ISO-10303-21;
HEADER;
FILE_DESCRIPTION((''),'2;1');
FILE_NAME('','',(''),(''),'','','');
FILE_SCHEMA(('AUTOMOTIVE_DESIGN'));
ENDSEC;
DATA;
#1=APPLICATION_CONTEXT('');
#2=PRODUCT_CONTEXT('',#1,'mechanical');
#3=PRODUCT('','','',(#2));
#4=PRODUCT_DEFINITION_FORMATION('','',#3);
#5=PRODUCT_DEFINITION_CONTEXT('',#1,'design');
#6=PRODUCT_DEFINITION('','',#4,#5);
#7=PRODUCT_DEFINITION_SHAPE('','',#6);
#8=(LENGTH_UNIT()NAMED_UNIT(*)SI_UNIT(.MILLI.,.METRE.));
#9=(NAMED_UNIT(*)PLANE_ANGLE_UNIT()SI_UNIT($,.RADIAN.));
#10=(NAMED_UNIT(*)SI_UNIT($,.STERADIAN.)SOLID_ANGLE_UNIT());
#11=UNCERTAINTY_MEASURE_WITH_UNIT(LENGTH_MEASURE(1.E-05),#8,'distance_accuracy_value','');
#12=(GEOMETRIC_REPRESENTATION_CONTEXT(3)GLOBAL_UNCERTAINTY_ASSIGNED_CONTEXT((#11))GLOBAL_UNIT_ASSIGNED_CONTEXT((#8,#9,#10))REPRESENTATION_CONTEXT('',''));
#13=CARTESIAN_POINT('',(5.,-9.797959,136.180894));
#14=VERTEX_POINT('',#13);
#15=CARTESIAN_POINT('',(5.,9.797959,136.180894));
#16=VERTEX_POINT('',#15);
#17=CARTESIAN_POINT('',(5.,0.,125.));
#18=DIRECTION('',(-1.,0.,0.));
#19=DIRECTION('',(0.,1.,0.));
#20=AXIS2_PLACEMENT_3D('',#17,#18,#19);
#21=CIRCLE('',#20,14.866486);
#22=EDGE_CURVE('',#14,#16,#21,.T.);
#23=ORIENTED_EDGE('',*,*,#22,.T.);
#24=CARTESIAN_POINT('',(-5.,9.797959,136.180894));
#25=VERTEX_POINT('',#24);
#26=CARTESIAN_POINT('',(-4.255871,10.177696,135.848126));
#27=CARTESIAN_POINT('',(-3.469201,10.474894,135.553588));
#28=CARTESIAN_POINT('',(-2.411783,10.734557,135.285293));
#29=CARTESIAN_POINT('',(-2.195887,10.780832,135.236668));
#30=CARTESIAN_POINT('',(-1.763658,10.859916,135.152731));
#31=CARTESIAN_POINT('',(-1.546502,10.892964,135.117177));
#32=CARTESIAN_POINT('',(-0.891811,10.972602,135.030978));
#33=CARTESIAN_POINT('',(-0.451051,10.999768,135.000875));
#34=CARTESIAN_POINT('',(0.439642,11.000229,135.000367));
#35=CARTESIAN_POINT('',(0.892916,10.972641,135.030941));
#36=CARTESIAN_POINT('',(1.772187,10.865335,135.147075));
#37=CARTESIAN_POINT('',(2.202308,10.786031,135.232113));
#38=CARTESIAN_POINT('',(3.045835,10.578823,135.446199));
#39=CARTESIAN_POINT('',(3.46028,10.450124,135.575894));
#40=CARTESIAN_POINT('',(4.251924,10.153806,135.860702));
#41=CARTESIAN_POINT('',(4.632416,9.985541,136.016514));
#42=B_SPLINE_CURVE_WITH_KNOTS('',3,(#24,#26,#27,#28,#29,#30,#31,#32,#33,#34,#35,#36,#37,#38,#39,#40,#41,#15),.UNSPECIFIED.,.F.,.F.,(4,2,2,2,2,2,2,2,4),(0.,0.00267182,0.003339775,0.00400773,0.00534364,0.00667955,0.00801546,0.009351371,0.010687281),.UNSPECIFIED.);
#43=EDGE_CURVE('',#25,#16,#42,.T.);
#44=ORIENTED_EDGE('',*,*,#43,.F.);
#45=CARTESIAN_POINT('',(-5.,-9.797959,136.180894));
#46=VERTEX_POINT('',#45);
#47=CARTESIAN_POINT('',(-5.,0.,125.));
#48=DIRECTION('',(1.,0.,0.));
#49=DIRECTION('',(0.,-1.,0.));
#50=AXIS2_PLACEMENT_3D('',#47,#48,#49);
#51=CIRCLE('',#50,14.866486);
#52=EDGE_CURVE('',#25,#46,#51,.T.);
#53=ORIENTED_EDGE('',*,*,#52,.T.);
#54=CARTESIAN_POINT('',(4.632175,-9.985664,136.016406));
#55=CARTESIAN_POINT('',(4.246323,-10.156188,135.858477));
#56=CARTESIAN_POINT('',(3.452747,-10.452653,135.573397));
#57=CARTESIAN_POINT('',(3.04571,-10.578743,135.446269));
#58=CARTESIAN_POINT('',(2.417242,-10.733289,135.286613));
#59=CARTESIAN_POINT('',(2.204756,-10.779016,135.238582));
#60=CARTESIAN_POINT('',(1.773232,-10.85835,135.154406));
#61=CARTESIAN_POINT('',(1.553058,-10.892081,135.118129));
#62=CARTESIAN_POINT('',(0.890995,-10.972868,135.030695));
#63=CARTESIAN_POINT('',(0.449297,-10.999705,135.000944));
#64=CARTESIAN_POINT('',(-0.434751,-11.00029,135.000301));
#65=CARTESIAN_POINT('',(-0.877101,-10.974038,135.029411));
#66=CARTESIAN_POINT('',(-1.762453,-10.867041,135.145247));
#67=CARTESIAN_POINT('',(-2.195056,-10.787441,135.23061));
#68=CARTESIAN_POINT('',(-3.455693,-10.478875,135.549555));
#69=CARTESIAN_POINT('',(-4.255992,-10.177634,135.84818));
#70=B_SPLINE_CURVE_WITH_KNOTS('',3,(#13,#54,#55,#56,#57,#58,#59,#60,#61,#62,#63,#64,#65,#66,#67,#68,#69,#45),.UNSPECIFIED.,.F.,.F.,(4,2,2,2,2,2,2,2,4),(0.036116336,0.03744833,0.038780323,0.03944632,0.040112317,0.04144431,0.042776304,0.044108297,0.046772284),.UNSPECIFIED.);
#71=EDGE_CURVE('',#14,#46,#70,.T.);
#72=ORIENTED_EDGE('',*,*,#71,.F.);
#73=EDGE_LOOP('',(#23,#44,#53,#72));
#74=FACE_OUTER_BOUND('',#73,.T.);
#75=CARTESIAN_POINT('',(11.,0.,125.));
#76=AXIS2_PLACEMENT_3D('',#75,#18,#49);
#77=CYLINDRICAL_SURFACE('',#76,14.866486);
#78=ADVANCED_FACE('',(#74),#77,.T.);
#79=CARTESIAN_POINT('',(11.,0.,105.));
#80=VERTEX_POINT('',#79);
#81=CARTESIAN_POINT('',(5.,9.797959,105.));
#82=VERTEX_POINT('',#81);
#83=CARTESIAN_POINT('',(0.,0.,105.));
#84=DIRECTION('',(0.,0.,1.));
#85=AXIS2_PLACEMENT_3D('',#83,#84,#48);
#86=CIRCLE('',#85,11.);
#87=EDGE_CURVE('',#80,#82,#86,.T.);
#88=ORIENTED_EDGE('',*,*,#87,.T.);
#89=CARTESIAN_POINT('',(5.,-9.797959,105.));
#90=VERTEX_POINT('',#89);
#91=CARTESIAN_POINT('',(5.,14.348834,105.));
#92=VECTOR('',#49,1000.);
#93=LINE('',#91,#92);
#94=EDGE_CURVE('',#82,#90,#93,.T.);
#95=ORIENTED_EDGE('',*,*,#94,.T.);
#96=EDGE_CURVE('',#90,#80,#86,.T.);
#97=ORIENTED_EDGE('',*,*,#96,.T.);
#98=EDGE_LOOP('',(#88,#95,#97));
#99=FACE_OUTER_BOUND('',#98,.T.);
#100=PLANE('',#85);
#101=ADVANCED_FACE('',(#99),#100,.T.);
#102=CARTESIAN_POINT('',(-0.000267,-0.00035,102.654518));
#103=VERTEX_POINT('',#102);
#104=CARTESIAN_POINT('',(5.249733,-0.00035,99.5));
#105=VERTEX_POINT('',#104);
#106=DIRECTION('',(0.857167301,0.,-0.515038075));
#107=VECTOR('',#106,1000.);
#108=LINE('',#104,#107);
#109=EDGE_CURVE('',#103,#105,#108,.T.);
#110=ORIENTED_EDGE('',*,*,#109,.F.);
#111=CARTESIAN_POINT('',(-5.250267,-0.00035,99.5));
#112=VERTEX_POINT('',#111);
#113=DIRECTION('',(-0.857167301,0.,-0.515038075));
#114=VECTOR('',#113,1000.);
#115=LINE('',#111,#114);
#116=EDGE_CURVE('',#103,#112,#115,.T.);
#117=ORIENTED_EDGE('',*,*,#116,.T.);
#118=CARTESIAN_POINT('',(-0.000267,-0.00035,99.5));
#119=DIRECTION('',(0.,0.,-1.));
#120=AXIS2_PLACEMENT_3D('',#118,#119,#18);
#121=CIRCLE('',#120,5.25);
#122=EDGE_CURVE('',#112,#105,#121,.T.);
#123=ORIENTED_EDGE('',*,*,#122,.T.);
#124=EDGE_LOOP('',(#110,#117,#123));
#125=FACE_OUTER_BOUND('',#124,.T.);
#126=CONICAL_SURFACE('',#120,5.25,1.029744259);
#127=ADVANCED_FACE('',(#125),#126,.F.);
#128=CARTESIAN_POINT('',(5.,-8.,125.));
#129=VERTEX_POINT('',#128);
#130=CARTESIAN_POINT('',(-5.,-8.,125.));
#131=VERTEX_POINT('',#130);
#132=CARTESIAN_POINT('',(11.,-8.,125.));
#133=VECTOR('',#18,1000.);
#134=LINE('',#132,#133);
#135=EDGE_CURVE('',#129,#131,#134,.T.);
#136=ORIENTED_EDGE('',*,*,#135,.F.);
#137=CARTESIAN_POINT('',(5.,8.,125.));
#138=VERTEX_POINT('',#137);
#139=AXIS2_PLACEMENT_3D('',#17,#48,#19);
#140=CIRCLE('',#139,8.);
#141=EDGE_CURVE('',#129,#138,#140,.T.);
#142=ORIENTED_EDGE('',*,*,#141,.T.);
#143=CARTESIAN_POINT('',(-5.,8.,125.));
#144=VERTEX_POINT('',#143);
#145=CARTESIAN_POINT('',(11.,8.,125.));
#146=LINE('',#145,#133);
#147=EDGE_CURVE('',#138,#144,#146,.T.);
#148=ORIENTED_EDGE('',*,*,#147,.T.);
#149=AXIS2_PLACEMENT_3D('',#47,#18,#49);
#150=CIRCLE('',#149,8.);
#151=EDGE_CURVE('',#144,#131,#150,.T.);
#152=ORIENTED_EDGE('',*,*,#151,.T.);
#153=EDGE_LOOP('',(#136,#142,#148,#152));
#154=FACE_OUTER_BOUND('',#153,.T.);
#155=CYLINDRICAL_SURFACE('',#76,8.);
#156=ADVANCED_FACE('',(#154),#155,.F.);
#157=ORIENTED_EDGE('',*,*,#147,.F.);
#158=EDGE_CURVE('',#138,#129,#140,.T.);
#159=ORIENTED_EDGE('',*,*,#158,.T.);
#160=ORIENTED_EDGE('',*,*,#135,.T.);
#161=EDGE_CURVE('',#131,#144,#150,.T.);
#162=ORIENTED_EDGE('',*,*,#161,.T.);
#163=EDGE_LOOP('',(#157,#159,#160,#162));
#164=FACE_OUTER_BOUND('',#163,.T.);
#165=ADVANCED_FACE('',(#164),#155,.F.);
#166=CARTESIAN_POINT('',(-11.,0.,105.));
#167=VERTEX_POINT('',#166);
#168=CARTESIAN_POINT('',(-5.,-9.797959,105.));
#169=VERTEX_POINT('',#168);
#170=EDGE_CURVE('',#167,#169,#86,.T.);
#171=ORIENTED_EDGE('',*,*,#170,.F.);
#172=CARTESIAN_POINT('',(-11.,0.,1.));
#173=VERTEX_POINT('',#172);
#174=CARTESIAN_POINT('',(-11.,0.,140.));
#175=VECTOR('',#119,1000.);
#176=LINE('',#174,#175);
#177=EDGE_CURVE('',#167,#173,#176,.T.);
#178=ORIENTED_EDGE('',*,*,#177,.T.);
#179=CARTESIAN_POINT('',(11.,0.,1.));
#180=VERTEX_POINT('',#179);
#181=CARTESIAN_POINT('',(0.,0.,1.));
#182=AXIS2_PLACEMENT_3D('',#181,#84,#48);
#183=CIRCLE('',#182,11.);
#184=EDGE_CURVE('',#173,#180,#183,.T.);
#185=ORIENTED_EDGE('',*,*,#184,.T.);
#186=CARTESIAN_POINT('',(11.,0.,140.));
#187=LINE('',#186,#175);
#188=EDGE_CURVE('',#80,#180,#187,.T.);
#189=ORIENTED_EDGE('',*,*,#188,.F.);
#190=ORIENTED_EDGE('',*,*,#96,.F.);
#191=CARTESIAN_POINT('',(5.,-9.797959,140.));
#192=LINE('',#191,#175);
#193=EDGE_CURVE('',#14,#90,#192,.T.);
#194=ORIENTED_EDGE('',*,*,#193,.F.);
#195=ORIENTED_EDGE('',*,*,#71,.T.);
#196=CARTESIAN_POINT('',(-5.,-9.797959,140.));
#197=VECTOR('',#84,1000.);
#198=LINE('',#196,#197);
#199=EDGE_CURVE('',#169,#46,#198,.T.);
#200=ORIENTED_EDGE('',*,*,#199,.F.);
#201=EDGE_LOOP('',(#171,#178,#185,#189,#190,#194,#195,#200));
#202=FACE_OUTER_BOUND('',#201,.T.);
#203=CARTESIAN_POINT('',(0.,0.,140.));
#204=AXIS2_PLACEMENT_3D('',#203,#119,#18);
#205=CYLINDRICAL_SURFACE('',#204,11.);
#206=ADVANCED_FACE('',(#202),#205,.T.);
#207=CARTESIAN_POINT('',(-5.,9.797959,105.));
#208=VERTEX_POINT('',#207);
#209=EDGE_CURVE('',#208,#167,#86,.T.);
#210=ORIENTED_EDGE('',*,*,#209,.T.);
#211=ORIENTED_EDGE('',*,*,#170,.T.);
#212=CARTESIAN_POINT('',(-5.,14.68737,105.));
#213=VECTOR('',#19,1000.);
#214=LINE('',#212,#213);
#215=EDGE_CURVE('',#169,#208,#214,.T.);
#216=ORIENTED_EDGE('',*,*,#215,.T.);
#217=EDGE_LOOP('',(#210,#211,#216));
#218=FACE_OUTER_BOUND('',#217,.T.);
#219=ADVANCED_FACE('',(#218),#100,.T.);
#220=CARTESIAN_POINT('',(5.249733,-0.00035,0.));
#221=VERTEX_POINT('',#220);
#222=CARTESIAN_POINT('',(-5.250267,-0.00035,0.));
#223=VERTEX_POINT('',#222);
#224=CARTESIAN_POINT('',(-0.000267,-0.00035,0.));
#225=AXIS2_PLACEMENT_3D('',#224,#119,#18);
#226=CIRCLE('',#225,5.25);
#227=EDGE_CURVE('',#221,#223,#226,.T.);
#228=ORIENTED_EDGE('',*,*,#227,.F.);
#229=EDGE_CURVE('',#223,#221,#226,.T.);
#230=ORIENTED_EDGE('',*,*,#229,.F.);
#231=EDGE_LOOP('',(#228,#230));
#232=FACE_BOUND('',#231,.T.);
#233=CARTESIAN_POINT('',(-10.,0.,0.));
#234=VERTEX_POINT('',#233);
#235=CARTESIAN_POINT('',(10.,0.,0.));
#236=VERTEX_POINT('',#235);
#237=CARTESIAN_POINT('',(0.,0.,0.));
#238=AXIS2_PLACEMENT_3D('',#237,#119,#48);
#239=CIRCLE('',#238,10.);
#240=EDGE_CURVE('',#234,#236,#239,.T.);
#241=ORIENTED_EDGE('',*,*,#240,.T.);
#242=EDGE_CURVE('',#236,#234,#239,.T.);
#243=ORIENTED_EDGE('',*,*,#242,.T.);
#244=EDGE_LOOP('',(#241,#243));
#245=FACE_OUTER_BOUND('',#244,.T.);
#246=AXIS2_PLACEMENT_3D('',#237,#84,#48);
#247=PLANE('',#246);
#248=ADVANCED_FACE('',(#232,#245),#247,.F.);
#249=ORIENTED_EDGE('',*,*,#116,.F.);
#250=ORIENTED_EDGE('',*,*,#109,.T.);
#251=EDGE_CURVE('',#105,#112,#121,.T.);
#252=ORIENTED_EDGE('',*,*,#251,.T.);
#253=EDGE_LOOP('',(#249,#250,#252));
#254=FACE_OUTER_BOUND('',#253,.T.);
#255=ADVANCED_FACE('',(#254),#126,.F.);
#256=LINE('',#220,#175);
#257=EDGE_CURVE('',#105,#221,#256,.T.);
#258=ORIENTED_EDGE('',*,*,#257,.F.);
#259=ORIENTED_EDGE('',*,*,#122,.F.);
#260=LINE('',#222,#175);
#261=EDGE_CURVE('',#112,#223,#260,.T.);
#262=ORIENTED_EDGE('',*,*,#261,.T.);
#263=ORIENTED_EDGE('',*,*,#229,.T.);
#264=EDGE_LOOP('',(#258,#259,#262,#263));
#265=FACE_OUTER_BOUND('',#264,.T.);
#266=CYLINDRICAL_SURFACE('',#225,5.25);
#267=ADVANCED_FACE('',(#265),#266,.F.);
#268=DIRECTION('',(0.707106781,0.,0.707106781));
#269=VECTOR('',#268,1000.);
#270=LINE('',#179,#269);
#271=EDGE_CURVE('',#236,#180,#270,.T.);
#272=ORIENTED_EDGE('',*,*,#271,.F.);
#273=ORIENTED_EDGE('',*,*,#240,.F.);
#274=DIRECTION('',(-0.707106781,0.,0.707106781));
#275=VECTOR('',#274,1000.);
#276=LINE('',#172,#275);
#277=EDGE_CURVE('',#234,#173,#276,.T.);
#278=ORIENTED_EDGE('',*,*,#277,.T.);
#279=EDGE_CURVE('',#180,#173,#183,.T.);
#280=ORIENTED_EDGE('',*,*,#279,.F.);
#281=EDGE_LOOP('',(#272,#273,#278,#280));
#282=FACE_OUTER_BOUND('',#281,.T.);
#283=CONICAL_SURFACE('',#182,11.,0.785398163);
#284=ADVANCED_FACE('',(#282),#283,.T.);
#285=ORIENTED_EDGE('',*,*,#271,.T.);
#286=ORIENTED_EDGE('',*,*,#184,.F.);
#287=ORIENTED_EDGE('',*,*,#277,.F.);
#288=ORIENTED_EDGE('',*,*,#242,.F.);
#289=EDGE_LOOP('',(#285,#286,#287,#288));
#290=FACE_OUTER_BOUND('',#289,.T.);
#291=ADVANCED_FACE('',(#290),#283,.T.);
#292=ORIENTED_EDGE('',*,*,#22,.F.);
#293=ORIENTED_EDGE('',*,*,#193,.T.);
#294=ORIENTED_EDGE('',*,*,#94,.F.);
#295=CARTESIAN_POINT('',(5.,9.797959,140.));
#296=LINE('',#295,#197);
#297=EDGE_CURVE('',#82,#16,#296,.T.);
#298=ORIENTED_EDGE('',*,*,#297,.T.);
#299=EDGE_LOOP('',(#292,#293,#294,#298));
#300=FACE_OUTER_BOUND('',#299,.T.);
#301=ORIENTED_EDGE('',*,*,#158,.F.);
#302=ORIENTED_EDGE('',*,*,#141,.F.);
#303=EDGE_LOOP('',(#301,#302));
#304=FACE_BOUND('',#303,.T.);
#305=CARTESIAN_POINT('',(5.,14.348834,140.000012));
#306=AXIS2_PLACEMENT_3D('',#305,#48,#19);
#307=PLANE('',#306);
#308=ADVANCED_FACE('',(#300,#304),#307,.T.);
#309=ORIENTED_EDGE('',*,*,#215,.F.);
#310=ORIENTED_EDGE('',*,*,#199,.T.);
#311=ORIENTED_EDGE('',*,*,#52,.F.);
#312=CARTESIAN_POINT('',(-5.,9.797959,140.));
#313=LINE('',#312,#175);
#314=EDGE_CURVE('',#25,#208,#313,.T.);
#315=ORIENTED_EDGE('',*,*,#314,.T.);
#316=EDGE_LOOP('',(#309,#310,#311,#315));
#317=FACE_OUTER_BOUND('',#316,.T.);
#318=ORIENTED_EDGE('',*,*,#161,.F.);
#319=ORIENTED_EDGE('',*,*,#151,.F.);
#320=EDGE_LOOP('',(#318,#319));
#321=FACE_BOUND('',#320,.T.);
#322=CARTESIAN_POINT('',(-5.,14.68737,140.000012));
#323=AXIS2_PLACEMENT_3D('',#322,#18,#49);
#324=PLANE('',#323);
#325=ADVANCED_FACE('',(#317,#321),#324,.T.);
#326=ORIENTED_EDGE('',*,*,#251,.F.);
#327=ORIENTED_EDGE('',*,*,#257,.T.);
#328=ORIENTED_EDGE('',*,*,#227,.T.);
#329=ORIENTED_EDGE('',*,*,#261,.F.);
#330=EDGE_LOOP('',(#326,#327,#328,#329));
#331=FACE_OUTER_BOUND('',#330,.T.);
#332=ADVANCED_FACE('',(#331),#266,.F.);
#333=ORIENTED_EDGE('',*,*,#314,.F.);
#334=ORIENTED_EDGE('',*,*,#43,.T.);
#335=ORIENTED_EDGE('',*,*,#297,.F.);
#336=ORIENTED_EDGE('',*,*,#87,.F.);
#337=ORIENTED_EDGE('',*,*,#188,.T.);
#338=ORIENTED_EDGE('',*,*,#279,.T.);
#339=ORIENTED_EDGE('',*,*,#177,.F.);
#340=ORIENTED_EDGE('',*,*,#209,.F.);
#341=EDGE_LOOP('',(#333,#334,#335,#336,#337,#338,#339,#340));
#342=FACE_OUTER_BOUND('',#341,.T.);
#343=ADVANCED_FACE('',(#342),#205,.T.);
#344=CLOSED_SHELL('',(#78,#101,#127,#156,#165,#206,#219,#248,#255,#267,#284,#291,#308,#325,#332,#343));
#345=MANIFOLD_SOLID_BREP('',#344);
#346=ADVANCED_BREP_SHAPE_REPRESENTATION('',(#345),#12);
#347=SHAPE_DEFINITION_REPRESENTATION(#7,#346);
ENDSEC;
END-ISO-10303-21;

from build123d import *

# Parameters (mm, degrees)
SKETCH1_R                  = 11
BOSS_EXTRUDE1_DEPTH        = 140
CUT_EXTRUDE1_DEPTH         = 141.861634237
CUT_EXTRUDE1_DEPTH_BACK    = 35
SKETCH2_W                  = 16.868879615
SKETCH2_H                  = 32.554880476
SKETCH2_W_2                = 13.301543069
SKETCH2_H_2                = 32.07054439
M12X1_5_TAPPED_HOLE1_D     = 10.5
M12X1_5_TAPPED_HOLE1_DEPTH = 99.5
M12X1_5_TAPPED_HOLE1_TIP   = 3.15451825
CHAMFER1_SIZE              = 1
SKETCH5_R                  = 8
CUT_EXTRUDE2_DEPTH         = 142.340015565


with BuildPart() as part:
    # Sketch1 → Boss-Extrude1 (new body)
    with BuildSketch(Plane.XY):
        Circle(SKETCH1_R)
    extrude(amount=BOSS_EXTRUDE1_DEPTH)

    # Sketch2 → Cut-Extrude1 (cut, two sides: drawn at the far end of the back side and taken through both)
    with BuildSketch(Plane.XY.offset(140).offset(-CUT_EXTRUDE1_DEPTH_BACK)):
        with Locations((13.434439808, -1.928606663)):
            Rectangle(SKETCH2_W, SKETCH2_H)
        with Locations((-11.650771535, -1.34790253)):
            Rectangle(SKETCH2_W_2, SKETCH2_H_2)
    extrude(amount=CUT_EXTRUDE1_DEPTH + CUT_EXTRUDE1_DEPTH_BACK, mode=Mode.SUBTRACT)

    # M12x1.5 Tapped Hole1
    with Locations(Plane(origin=(-0.000266702, -0.000350185, 0), x_dir=(-1, 0, 0), z_dir=(0, 0, -1))):
        with Locations((0, 0)):
            Hole(M12X1_5_TAPPED_HOLE1_D / 2, depth=M12X1_5_TAPPED_HOLE1_DEPTH)
            with Locations((0, 0, -(M12X1_5_TAPPED_HOLE1_DEPTH + M12X1_5_TAPPED_HOLE1_TIP / 2))):  # 118° drill point
                Cone(0, M12X1_5_TAPPED_HOLE1_D / 2, M12X1_5_TAPPED_HOLE1_TIP, mode=Mode.SUBTRACT)

    # Chamfer1
    chamfer1_edges = [part.edges().sort_by_distance(p)[0] for p in [
        (-11, 0, 0),
    ]]
    chamfer(chamfer1_edges, length=CHAMFER1_SIZE)

    # Sketch5 → Cut-Extrude2 (cut, through all)
    with BuildSketch(Plane.ZY.offset(5)):
        with Locations(Location((125, 0, 0), (0, 0, 270))):
            Circle(SKETCH5_R)
        with BuildLine():
            Line((125, 14.866485564), (182.888016926, 36.743525749))
            Line((182.888016926, 36.743525749), (236.673487902, -7.349157171))
            Line((236.673487902, -7.349157171), (192.77085965, -51.061730756))
            Line((192.77085965, -51.061730756), (125, -14.866485564))
            ThreePointArc((125, -14.866485564), (139.866485564, 0), (125, 14.866485564))
        make_face()
    extrude(amount=-CUT_EXTRUDE2_DEPTH, mode=Mode.SUBTRACT)


solid = part.part
